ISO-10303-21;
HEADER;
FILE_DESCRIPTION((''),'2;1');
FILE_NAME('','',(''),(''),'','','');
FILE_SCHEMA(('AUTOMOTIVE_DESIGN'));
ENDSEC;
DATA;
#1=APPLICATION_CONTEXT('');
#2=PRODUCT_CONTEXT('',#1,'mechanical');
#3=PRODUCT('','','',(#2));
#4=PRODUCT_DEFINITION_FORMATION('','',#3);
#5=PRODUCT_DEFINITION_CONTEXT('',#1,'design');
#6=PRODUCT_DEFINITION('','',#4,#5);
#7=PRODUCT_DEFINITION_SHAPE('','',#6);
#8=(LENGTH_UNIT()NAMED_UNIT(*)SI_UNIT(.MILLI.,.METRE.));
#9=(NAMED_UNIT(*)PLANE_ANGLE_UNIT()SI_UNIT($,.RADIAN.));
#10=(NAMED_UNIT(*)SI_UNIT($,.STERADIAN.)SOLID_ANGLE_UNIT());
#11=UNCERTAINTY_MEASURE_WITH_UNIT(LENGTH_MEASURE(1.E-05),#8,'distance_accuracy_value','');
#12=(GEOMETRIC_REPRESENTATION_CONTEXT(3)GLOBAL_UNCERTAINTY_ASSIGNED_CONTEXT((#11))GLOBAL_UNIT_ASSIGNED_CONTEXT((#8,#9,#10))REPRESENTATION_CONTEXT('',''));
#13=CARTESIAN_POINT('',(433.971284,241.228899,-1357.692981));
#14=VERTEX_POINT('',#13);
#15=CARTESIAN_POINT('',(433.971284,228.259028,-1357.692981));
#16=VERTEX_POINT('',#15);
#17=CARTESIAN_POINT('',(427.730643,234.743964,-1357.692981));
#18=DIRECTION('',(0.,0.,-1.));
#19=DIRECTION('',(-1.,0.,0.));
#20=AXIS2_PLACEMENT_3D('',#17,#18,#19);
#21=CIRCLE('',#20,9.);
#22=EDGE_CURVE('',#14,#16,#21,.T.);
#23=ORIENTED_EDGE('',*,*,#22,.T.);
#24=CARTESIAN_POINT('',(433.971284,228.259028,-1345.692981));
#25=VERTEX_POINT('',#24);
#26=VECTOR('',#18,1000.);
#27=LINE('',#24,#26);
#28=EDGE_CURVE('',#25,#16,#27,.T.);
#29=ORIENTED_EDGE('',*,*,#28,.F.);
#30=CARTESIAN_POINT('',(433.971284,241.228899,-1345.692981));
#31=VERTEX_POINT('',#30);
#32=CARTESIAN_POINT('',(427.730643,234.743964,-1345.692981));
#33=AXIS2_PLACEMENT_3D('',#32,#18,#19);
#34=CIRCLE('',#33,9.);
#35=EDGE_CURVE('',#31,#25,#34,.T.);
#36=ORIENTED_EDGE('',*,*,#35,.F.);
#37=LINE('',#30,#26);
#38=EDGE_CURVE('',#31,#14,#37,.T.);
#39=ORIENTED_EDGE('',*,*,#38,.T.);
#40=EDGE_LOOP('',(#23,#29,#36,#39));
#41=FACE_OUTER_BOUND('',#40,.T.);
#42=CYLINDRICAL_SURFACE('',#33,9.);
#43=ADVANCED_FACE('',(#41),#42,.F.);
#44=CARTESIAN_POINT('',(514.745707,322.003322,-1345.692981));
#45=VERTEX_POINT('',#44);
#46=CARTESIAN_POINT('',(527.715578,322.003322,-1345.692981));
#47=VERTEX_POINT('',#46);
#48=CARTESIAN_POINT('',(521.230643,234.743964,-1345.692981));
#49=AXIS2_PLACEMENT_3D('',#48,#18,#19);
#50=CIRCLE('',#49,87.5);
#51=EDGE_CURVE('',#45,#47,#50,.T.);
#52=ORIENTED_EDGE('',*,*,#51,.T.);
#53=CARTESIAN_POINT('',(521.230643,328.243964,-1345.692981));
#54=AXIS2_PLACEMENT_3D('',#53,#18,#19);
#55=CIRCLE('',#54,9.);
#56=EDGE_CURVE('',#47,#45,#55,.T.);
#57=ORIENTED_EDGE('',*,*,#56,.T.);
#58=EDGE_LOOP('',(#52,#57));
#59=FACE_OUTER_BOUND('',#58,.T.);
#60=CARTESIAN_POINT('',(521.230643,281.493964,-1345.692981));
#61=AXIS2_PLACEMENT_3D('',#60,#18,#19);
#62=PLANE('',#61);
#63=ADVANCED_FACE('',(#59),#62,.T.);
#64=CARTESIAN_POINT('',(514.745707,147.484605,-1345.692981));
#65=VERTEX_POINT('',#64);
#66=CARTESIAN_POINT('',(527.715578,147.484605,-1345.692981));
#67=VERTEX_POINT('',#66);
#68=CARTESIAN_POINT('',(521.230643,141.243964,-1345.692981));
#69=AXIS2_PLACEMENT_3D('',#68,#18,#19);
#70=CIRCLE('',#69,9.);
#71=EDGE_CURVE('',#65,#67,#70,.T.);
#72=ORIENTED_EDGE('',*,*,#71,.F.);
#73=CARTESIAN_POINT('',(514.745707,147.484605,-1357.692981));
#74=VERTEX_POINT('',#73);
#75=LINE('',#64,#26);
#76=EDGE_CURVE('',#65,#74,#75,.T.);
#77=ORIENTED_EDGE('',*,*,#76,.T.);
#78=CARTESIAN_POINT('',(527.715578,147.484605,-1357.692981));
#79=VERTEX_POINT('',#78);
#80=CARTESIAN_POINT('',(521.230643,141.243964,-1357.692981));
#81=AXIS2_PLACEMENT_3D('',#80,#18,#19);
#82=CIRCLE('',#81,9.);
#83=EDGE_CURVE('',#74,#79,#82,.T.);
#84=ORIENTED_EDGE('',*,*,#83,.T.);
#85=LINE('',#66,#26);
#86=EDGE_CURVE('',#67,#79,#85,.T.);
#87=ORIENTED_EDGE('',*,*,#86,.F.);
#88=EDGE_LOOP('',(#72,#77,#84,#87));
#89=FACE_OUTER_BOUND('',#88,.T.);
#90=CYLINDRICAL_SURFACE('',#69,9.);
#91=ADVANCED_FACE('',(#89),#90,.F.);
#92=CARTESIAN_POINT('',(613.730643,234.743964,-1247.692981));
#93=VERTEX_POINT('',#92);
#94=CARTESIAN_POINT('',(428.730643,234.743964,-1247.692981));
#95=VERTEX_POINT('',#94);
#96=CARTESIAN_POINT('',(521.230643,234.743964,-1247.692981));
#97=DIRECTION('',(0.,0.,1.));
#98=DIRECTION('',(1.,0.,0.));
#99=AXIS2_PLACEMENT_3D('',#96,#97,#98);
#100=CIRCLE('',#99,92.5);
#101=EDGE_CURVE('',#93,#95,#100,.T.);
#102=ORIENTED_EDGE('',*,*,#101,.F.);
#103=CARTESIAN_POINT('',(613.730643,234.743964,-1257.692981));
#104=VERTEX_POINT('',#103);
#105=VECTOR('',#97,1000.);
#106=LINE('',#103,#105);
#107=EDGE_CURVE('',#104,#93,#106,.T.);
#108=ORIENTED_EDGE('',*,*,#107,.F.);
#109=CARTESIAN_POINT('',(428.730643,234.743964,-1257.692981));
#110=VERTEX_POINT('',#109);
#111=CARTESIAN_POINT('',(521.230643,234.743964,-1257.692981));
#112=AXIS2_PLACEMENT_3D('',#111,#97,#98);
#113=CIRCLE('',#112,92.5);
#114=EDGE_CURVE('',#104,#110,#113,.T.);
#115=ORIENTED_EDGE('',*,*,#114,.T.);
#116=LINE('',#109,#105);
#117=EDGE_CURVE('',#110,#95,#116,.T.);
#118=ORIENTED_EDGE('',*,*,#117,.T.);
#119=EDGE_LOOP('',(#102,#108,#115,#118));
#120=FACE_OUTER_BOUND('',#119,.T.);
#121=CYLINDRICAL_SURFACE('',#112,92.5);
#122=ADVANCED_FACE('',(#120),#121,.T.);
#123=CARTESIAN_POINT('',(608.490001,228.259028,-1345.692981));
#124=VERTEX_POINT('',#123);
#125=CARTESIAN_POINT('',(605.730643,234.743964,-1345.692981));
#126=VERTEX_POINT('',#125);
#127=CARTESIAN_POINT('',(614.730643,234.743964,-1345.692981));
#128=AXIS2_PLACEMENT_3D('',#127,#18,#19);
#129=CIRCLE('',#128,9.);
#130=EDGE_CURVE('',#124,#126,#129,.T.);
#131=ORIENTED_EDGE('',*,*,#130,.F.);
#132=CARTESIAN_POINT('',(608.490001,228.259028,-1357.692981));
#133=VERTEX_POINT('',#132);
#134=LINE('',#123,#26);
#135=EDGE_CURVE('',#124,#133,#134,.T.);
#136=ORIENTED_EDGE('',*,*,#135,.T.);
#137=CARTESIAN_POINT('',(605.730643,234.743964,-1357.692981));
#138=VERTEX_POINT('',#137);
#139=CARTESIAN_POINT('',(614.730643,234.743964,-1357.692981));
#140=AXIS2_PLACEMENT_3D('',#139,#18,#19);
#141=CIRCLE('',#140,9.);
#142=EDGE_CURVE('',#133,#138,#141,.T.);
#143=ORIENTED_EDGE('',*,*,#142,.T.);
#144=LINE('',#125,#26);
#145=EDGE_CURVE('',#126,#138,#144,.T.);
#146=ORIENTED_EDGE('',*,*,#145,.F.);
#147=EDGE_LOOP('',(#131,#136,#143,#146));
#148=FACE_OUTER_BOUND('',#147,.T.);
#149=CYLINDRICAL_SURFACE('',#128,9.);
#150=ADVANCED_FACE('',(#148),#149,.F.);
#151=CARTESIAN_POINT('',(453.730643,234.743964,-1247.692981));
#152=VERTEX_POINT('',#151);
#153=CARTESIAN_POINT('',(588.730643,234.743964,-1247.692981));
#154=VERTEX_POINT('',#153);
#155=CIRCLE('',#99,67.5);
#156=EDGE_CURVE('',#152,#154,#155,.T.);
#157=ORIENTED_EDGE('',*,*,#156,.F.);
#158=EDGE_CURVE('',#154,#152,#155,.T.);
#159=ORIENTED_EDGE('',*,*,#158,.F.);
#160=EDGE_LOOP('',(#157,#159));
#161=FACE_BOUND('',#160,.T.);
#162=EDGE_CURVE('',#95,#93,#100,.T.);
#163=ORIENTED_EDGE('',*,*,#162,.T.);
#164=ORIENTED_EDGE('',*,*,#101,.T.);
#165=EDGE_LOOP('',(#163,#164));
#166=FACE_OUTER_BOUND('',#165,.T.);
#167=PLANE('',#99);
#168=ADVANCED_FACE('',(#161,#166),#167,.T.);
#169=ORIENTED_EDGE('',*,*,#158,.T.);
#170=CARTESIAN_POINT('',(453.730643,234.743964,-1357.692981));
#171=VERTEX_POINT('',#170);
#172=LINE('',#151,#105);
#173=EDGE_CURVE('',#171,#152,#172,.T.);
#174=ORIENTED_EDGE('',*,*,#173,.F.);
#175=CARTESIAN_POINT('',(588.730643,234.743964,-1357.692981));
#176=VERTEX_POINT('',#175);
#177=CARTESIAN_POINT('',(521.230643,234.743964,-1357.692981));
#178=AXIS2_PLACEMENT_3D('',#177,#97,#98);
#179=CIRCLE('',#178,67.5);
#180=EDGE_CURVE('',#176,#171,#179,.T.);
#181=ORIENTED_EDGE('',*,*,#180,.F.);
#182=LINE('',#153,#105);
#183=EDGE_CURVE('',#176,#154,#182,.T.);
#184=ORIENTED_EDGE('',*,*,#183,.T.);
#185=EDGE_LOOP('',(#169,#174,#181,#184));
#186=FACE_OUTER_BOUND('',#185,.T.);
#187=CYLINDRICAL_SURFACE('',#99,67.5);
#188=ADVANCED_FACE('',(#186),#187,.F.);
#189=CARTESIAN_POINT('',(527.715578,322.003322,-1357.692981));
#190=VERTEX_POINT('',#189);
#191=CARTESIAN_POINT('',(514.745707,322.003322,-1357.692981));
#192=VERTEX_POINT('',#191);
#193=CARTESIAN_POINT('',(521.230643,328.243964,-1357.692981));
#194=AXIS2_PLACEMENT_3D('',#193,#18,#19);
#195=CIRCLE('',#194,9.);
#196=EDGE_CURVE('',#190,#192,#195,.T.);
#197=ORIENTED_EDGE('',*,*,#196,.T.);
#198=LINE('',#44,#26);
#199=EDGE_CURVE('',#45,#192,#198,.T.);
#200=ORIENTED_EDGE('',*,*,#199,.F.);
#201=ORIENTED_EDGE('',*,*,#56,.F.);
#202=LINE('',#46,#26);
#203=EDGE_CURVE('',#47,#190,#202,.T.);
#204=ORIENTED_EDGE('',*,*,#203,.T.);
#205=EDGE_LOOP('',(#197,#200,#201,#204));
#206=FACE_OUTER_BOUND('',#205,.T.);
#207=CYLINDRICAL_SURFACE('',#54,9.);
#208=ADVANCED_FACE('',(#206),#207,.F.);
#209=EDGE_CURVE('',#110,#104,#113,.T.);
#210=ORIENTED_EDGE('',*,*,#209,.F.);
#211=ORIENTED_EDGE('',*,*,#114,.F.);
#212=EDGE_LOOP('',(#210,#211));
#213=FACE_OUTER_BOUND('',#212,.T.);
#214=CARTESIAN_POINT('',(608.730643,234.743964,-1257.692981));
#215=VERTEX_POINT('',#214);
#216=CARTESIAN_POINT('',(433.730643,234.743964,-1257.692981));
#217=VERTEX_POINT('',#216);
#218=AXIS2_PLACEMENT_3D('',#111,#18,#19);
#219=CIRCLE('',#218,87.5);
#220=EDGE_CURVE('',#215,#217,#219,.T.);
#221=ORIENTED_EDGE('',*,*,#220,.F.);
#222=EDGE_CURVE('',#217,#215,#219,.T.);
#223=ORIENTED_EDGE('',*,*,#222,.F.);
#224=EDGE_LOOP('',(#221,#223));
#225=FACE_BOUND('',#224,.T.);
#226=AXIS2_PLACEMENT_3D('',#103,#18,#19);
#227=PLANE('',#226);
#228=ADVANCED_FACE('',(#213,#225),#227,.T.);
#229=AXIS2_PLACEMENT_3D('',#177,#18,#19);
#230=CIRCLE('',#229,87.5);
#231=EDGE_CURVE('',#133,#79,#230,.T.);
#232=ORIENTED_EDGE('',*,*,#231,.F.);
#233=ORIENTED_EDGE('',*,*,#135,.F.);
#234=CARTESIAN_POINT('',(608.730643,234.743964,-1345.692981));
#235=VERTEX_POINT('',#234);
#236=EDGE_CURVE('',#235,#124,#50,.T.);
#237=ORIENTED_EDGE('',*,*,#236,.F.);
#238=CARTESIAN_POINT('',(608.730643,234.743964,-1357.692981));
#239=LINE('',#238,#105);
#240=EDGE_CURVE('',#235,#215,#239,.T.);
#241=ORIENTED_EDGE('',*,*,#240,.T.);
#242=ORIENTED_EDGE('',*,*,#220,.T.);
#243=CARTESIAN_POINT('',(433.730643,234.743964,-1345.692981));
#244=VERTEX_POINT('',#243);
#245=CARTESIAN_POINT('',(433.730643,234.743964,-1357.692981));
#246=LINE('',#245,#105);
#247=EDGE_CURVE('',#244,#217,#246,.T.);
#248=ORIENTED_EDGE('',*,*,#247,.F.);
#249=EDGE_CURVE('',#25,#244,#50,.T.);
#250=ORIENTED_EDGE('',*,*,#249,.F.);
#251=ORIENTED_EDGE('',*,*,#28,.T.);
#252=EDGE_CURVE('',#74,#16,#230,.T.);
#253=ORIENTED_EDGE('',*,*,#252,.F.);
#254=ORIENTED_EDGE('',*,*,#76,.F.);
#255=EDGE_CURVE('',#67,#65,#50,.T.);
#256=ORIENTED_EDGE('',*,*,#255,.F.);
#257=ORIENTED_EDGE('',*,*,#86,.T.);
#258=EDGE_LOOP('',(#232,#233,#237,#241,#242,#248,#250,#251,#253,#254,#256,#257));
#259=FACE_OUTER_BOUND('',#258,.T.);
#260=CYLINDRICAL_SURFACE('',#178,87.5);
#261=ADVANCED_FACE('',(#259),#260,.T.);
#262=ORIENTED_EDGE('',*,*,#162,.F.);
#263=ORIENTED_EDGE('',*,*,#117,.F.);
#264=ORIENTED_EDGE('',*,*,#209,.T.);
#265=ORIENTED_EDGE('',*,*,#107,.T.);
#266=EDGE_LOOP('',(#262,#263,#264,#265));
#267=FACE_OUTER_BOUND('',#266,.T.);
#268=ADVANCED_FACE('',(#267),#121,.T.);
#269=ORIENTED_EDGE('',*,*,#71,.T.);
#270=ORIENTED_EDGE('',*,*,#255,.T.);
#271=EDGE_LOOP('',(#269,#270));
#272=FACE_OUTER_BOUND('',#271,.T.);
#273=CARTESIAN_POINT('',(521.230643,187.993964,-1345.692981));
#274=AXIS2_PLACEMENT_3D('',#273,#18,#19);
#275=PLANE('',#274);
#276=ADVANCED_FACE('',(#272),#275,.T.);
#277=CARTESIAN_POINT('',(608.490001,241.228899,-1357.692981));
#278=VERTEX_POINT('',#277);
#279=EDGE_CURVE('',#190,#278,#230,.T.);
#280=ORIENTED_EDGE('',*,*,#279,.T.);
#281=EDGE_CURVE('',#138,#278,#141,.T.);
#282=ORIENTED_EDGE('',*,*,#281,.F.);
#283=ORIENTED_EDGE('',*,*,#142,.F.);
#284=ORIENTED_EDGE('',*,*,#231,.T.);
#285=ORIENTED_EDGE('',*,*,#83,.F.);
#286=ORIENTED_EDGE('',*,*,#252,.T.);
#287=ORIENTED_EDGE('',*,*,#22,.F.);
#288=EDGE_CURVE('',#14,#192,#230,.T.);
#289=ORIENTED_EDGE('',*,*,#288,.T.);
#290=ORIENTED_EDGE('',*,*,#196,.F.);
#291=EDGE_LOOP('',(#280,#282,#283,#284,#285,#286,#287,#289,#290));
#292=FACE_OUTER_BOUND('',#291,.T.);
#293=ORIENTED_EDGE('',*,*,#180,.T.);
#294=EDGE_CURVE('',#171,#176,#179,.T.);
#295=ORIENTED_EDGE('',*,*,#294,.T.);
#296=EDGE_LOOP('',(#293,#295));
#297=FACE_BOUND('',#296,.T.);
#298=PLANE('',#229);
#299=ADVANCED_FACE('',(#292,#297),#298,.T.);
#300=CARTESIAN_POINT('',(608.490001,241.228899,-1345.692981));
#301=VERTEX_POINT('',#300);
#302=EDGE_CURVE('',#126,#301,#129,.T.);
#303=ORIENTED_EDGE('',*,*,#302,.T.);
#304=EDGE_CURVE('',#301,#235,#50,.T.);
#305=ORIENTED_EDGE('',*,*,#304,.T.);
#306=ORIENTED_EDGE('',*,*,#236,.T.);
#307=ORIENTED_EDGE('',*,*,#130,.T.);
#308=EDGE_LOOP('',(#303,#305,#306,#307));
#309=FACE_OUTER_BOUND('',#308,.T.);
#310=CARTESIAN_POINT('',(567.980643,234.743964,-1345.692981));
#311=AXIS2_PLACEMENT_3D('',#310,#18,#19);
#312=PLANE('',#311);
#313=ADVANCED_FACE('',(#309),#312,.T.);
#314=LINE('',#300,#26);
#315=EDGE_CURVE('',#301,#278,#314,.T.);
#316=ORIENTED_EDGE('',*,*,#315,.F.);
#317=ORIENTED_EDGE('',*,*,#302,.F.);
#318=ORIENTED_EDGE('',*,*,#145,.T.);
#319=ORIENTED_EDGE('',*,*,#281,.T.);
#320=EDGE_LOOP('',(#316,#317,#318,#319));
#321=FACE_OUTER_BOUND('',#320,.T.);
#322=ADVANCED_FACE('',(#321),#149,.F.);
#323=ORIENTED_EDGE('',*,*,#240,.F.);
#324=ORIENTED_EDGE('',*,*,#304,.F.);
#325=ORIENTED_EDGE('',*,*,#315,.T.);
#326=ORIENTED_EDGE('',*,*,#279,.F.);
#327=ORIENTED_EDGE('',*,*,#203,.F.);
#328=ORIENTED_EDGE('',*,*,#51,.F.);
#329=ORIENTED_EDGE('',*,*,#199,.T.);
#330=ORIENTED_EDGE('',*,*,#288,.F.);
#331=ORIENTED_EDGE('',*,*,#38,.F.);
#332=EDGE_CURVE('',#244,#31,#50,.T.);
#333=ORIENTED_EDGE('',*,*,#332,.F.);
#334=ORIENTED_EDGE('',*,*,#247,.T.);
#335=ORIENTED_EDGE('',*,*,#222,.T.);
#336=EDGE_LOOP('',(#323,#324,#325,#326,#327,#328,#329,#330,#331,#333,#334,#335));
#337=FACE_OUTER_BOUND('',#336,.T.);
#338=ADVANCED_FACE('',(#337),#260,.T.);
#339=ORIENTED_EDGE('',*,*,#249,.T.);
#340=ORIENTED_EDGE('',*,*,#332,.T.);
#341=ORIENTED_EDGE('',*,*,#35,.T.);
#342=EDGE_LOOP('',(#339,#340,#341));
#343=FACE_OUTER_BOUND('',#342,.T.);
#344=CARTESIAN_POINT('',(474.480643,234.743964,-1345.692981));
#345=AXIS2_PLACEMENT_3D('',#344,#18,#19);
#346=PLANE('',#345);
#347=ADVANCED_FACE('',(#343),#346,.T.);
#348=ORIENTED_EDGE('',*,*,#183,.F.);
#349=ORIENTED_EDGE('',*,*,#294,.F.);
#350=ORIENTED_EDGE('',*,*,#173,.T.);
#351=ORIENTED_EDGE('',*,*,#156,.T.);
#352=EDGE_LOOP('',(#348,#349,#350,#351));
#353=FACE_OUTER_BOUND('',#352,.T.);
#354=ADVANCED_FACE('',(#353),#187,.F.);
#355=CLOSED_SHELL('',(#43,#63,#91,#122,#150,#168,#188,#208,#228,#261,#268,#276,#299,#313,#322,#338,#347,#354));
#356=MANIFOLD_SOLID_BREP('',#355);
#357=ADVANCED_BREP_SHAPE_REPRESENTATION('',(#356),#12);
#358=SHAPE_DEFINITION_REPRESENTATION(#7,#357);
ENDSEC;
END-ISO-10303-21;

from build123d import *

# Parameters (mm, degrees)
SKETCH1_W           = 92.5
SKETCH1_H           = 10
SKETCH2_R           = 87.5
BOSS_EXTRUDE1_DEPTH = 100
CUT_EXTRUDE1_START  = -12
CUT_EXTRUDE1_DEPTH  = 12
CUT_EXTRUDE2_START  = -12
CUT_EXTRUDE2_DEPTH  = 12
CUT_EXTRUDE3_START  = -12
CUT_EXTRUDE3_DEPTH  = 12
CUT_EXTRUDE4_START  = -12
CUT_EXTRUDE4_DEPTH  = 12
HOLE1_D             = 135


with BuildPart() as part:
    # Sketch1 → Revolve1 (revolve)
    with BuildSketch(Plane(origin=(0, 234.743963655, 0), x_dir=(1, 0, 0), z_dir=(0, 1, 0))):
        with Locations((567.480642584, 1252.692981355)):
            Rectangle(SKETCH1_W, SKETCH1_H)
    revolve(axis=Axis((521.230642584, 234.743963655, -1257.692981355), (0, 0, 1)))

    # Sketch2 → Boss-Extrude1 (add)
    with BuildSketch(Plane(origin=(0, 0, -1257.692981355), x_dir=(-1, 0, 0), z_dir=(0, 0, -1))):
        with Locations((-521.230642584, 234.743963655)):
            Circle(SKETCH2_R)
    extrude(amount=BOSS_EXTRUDE1_DEPTH)

    # Sketch3 → Cut-Extrude1 (cut)
    with BuildSketch(Plane(origin=(0, 0, -1357.692981355), x_dir=(-1, 0, 0), z_dir=(0, 0, -1)).offset(CUT_EXTRUDE1_START)):
        with BuildLine():
            ThreePointArc((-433.971284296, 241.228899354), (-436.730642584, 234.743963655), (-433.971284296, 228.259027955))
            ThreePointArc((-433.971284296, 228.259027955), (-433.730642584, 234.743963655), (-433.971284296, 241.228899354))
        make_face()
    extrude(amount=CUT_EXTRUDE1_DEPTH, mode=Mode.SUBTRACT)

    # Sketch4 → Cut-Extrude2 (cut)
    with BuildSketch(Plane(origin=(0, 0, -1357.692981355), x_dir=(-1, 0, 0), z_dir=(0, 0, -1)).offset(CUT_EXTRUDE2_START)):
        with BuildLine():
            ThreePointArc((-514.745706884, 147.484605366), (-521.230642584, 150.243963655), (-527.715578284, 147.484605366))
            ThreePointArc((-527.715578284, 147.484605366), (-521.230642584, 147.243963655), (-514.745706884, 147.484605366))
        make_face()
    extrude(amount=CUT_EXTRUDE2_DEPTH, mode=Mode.SUBTRACT)

    # Sketch5 → Cut-Extrude3 (cut)
    with BuildSketch(Plane(origin=(0, 0, -1357.692981355), x_dir=(-1, 0, 0), z_dir=(0, 0, -1)).offset(CUT_EXTRUDE3_START)):
        with BuildLine():
            ThreePointArc((-527.715578284, 322.003321943), (-521.230642584, 319.243963655), (-514.745706884, 322.003321943))
            ThreePointArc((-514.745706884, 322.003321943), (-521.230642584, 322.243963655), (-527.715578284, 322.003321943))
        make_face()
    extrude(amount=CUT_EXTRUDE3_DEPTH, mode=Mode.SUBTRACT)

    # Sketch6 → Cut-Extrude4 (cut)
    with BuildSketch(Plane(origin=(0, 0, -1357.692981355), x_dir=(-1, 0, 0), z_dir=(0, 0, -1)).offset(CUT_EXTRUDE4_START)):
        with BuildLine():
            ThreePointArc((-608.490000873, 228.259027955), (-605.730642584, 234.743963654), (-608.490000873, 241.228899354))
            ThreePointArc((-608.490000873, 241.228899354), (-608.730642584, 234.743963654), (-608.490000873, 228.259027955))
        make_face()
    extrude(amount=CUT_EXTRUDE4_DEPTH, mode=Mode.SUBTRACT)

    # Hole1 (through all)
    with Locations(Plane.XY.offset(-1247.692981355)):
        with Locations((521.230642584, 234.743963655)):
            Hole(HOLE1_D / 2)


solid = part.part
